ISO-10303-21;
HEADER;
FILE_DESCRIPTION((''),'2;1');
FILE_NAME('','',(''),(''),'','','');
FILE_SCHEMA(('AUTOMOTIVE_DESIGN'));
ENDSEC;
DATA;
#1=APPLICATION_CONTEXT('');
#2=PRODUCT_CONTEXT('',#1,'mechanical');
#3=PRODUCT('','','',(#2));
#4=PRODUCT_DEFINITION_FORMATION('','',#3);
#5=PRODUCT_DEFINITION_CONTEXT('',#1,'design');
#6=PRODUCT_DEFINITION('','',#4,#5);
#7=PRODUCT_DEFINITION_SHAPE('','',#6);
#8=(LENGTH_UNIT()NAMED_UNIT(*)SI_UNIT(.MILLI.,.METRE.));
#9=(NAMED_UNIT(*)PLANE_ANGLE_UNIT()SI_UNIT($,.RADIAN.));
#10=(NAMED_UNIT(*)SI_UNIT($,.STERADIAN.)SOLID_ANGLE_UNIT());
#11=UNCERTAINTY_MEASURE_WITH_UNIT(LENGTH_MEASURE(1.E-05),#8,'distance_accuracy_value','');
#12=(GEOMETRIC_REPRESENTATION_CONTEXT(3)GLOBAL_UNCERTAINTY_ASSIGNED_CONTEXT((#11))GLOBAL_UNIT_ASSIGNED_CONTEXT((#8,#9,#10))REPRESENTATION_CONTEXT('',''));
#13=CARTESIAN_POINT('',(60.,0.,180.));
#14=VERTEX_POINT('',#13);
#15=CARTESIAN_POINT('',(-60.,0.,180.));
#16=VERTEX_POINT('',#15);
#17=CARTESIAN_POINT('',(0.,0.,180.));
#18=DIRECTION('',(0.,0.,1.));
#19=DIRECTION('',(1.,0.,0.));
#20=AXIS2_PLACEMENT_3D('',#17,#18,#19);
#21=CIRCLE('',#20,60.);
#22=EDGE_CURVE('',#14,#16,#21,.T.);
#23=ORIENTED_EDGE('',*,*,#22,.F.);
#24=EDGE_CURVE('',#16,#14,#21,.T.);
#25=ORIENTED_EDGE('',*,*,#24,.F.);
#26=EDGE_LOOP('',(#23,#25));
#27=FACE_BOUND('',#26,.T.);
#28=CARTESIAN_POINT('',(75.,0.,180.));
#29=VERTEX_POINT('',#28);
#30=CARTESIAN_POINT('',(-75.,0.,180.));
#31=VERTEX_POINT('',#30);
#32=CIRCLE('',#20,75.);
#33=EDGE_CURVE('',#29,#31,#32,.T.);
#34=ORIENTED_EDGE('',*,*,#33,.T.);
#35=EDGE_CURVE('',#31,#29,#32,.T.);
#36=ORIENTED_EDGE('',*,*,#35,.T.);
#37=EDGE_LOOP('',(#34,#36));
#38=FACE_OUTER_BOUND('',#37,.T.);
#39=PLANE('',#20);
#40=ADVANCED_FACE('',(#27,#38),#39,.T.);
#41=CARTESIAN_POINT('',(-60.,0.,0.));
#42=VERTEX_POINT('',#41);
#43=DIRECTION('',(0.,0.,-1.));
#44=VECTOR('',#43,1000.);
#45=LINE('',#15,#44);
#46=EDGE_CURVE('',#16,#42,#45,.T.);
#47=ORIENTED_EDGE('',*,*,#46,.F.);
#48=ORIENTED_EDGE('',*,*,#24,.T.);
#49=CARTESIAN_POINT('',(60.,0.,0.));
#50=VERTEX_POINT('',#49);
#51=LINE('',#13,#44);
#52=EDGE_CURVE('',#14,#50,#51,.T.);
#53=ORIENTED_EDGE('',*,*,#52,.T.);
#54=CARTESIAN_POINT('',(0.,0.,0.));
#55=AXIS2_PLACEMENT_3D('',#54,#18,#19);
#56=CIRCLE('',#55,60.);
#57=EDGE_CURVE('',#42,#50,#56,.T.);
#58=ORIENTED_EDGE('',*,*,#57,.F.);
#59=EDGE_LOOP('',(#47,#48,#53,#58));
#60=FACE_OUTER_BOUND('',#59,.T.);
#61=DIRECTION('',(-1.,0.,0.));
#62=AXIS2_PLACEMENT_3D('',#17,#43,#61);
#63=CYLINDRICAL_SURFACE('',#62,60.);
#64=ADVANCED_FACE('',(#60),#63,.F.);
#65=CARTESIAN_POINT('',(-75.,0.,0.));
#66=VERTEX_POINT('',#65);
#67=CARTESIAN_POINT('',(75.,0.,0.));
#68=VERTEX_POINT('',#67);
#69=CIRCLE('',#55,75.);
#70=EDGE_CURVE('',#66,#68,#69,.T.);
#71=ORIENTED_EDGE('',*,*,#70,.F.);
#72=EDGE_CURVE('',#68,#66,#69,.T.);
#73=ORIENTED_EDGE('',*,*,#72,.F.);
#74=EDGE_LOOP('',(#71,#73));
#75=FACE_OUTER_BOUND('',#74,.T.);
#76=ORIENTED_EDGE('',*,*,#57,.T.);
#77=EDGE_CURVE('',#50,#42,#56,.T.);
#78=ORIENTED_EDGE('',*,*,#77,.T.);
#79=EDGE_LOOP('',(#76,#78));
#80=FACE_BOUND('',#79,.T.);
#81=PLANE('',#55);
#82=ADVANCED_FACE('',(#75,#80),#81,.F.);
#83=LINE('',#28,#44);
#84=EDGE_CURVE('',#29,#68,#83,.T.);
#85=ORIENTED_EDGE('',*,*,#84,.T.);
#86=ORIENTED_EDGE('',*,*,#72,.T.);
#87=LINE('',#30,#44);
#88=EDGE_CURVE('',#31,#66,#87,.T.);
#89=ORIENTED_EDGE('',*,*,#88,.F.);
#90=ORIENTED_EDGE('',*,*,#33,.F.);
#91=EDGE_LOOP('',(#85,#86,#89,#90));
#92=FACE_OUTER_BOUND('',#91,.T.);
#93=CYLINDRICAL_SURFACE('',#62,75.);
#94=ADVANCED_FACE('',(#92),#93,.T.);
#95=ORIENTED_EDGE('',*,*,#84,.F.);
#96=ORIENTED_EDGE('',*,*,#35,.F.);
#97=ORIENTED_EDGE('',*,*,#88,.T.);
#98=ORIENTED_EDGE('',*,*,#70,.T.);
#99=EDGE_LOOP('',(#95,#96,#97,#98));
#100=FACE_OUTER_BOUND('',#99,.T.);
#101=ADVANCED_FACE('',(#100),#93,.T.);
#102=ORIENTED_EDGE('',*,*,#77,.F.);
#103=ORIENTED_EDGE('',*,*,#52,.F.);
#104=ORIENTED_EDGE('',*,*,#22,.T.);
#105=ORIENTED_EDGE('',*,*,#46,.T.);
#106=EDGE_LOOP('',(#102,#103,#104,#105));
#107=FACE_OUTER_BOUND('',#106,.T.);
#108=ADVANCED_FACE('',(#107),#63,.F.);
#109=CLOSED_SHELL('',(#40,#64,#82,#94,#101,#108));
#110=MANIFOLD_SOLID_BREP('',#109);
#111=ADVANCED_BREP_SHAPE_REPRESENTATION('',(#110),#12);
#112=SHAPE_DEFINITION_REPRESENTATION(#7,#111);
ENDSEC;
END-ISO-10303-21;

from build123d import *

# Parameters (mm, degrees)
SKETCH1_R           = 75
SKETCH1_R_2         = 60
BOSS_EXTRUDE1_DEPTH = 180


with BuildPart() as part:
    # Sketch1 → Boss-Extrude1 (new body)
    with BuildSketch(Plane.XY):
        with Locations(Location((0, 0, 0), (0, 0, 180))):
            Circle(SKETCH1_R)
        with Locations(Location((0, 0, 0), (0, 0, 180))):
            Circle(SKETCH1_R_2, mode=Mode.SUBTRACT)
    extrude(amount=BOSS_EXTRUDE1_DEPTH)


solid = part.part
